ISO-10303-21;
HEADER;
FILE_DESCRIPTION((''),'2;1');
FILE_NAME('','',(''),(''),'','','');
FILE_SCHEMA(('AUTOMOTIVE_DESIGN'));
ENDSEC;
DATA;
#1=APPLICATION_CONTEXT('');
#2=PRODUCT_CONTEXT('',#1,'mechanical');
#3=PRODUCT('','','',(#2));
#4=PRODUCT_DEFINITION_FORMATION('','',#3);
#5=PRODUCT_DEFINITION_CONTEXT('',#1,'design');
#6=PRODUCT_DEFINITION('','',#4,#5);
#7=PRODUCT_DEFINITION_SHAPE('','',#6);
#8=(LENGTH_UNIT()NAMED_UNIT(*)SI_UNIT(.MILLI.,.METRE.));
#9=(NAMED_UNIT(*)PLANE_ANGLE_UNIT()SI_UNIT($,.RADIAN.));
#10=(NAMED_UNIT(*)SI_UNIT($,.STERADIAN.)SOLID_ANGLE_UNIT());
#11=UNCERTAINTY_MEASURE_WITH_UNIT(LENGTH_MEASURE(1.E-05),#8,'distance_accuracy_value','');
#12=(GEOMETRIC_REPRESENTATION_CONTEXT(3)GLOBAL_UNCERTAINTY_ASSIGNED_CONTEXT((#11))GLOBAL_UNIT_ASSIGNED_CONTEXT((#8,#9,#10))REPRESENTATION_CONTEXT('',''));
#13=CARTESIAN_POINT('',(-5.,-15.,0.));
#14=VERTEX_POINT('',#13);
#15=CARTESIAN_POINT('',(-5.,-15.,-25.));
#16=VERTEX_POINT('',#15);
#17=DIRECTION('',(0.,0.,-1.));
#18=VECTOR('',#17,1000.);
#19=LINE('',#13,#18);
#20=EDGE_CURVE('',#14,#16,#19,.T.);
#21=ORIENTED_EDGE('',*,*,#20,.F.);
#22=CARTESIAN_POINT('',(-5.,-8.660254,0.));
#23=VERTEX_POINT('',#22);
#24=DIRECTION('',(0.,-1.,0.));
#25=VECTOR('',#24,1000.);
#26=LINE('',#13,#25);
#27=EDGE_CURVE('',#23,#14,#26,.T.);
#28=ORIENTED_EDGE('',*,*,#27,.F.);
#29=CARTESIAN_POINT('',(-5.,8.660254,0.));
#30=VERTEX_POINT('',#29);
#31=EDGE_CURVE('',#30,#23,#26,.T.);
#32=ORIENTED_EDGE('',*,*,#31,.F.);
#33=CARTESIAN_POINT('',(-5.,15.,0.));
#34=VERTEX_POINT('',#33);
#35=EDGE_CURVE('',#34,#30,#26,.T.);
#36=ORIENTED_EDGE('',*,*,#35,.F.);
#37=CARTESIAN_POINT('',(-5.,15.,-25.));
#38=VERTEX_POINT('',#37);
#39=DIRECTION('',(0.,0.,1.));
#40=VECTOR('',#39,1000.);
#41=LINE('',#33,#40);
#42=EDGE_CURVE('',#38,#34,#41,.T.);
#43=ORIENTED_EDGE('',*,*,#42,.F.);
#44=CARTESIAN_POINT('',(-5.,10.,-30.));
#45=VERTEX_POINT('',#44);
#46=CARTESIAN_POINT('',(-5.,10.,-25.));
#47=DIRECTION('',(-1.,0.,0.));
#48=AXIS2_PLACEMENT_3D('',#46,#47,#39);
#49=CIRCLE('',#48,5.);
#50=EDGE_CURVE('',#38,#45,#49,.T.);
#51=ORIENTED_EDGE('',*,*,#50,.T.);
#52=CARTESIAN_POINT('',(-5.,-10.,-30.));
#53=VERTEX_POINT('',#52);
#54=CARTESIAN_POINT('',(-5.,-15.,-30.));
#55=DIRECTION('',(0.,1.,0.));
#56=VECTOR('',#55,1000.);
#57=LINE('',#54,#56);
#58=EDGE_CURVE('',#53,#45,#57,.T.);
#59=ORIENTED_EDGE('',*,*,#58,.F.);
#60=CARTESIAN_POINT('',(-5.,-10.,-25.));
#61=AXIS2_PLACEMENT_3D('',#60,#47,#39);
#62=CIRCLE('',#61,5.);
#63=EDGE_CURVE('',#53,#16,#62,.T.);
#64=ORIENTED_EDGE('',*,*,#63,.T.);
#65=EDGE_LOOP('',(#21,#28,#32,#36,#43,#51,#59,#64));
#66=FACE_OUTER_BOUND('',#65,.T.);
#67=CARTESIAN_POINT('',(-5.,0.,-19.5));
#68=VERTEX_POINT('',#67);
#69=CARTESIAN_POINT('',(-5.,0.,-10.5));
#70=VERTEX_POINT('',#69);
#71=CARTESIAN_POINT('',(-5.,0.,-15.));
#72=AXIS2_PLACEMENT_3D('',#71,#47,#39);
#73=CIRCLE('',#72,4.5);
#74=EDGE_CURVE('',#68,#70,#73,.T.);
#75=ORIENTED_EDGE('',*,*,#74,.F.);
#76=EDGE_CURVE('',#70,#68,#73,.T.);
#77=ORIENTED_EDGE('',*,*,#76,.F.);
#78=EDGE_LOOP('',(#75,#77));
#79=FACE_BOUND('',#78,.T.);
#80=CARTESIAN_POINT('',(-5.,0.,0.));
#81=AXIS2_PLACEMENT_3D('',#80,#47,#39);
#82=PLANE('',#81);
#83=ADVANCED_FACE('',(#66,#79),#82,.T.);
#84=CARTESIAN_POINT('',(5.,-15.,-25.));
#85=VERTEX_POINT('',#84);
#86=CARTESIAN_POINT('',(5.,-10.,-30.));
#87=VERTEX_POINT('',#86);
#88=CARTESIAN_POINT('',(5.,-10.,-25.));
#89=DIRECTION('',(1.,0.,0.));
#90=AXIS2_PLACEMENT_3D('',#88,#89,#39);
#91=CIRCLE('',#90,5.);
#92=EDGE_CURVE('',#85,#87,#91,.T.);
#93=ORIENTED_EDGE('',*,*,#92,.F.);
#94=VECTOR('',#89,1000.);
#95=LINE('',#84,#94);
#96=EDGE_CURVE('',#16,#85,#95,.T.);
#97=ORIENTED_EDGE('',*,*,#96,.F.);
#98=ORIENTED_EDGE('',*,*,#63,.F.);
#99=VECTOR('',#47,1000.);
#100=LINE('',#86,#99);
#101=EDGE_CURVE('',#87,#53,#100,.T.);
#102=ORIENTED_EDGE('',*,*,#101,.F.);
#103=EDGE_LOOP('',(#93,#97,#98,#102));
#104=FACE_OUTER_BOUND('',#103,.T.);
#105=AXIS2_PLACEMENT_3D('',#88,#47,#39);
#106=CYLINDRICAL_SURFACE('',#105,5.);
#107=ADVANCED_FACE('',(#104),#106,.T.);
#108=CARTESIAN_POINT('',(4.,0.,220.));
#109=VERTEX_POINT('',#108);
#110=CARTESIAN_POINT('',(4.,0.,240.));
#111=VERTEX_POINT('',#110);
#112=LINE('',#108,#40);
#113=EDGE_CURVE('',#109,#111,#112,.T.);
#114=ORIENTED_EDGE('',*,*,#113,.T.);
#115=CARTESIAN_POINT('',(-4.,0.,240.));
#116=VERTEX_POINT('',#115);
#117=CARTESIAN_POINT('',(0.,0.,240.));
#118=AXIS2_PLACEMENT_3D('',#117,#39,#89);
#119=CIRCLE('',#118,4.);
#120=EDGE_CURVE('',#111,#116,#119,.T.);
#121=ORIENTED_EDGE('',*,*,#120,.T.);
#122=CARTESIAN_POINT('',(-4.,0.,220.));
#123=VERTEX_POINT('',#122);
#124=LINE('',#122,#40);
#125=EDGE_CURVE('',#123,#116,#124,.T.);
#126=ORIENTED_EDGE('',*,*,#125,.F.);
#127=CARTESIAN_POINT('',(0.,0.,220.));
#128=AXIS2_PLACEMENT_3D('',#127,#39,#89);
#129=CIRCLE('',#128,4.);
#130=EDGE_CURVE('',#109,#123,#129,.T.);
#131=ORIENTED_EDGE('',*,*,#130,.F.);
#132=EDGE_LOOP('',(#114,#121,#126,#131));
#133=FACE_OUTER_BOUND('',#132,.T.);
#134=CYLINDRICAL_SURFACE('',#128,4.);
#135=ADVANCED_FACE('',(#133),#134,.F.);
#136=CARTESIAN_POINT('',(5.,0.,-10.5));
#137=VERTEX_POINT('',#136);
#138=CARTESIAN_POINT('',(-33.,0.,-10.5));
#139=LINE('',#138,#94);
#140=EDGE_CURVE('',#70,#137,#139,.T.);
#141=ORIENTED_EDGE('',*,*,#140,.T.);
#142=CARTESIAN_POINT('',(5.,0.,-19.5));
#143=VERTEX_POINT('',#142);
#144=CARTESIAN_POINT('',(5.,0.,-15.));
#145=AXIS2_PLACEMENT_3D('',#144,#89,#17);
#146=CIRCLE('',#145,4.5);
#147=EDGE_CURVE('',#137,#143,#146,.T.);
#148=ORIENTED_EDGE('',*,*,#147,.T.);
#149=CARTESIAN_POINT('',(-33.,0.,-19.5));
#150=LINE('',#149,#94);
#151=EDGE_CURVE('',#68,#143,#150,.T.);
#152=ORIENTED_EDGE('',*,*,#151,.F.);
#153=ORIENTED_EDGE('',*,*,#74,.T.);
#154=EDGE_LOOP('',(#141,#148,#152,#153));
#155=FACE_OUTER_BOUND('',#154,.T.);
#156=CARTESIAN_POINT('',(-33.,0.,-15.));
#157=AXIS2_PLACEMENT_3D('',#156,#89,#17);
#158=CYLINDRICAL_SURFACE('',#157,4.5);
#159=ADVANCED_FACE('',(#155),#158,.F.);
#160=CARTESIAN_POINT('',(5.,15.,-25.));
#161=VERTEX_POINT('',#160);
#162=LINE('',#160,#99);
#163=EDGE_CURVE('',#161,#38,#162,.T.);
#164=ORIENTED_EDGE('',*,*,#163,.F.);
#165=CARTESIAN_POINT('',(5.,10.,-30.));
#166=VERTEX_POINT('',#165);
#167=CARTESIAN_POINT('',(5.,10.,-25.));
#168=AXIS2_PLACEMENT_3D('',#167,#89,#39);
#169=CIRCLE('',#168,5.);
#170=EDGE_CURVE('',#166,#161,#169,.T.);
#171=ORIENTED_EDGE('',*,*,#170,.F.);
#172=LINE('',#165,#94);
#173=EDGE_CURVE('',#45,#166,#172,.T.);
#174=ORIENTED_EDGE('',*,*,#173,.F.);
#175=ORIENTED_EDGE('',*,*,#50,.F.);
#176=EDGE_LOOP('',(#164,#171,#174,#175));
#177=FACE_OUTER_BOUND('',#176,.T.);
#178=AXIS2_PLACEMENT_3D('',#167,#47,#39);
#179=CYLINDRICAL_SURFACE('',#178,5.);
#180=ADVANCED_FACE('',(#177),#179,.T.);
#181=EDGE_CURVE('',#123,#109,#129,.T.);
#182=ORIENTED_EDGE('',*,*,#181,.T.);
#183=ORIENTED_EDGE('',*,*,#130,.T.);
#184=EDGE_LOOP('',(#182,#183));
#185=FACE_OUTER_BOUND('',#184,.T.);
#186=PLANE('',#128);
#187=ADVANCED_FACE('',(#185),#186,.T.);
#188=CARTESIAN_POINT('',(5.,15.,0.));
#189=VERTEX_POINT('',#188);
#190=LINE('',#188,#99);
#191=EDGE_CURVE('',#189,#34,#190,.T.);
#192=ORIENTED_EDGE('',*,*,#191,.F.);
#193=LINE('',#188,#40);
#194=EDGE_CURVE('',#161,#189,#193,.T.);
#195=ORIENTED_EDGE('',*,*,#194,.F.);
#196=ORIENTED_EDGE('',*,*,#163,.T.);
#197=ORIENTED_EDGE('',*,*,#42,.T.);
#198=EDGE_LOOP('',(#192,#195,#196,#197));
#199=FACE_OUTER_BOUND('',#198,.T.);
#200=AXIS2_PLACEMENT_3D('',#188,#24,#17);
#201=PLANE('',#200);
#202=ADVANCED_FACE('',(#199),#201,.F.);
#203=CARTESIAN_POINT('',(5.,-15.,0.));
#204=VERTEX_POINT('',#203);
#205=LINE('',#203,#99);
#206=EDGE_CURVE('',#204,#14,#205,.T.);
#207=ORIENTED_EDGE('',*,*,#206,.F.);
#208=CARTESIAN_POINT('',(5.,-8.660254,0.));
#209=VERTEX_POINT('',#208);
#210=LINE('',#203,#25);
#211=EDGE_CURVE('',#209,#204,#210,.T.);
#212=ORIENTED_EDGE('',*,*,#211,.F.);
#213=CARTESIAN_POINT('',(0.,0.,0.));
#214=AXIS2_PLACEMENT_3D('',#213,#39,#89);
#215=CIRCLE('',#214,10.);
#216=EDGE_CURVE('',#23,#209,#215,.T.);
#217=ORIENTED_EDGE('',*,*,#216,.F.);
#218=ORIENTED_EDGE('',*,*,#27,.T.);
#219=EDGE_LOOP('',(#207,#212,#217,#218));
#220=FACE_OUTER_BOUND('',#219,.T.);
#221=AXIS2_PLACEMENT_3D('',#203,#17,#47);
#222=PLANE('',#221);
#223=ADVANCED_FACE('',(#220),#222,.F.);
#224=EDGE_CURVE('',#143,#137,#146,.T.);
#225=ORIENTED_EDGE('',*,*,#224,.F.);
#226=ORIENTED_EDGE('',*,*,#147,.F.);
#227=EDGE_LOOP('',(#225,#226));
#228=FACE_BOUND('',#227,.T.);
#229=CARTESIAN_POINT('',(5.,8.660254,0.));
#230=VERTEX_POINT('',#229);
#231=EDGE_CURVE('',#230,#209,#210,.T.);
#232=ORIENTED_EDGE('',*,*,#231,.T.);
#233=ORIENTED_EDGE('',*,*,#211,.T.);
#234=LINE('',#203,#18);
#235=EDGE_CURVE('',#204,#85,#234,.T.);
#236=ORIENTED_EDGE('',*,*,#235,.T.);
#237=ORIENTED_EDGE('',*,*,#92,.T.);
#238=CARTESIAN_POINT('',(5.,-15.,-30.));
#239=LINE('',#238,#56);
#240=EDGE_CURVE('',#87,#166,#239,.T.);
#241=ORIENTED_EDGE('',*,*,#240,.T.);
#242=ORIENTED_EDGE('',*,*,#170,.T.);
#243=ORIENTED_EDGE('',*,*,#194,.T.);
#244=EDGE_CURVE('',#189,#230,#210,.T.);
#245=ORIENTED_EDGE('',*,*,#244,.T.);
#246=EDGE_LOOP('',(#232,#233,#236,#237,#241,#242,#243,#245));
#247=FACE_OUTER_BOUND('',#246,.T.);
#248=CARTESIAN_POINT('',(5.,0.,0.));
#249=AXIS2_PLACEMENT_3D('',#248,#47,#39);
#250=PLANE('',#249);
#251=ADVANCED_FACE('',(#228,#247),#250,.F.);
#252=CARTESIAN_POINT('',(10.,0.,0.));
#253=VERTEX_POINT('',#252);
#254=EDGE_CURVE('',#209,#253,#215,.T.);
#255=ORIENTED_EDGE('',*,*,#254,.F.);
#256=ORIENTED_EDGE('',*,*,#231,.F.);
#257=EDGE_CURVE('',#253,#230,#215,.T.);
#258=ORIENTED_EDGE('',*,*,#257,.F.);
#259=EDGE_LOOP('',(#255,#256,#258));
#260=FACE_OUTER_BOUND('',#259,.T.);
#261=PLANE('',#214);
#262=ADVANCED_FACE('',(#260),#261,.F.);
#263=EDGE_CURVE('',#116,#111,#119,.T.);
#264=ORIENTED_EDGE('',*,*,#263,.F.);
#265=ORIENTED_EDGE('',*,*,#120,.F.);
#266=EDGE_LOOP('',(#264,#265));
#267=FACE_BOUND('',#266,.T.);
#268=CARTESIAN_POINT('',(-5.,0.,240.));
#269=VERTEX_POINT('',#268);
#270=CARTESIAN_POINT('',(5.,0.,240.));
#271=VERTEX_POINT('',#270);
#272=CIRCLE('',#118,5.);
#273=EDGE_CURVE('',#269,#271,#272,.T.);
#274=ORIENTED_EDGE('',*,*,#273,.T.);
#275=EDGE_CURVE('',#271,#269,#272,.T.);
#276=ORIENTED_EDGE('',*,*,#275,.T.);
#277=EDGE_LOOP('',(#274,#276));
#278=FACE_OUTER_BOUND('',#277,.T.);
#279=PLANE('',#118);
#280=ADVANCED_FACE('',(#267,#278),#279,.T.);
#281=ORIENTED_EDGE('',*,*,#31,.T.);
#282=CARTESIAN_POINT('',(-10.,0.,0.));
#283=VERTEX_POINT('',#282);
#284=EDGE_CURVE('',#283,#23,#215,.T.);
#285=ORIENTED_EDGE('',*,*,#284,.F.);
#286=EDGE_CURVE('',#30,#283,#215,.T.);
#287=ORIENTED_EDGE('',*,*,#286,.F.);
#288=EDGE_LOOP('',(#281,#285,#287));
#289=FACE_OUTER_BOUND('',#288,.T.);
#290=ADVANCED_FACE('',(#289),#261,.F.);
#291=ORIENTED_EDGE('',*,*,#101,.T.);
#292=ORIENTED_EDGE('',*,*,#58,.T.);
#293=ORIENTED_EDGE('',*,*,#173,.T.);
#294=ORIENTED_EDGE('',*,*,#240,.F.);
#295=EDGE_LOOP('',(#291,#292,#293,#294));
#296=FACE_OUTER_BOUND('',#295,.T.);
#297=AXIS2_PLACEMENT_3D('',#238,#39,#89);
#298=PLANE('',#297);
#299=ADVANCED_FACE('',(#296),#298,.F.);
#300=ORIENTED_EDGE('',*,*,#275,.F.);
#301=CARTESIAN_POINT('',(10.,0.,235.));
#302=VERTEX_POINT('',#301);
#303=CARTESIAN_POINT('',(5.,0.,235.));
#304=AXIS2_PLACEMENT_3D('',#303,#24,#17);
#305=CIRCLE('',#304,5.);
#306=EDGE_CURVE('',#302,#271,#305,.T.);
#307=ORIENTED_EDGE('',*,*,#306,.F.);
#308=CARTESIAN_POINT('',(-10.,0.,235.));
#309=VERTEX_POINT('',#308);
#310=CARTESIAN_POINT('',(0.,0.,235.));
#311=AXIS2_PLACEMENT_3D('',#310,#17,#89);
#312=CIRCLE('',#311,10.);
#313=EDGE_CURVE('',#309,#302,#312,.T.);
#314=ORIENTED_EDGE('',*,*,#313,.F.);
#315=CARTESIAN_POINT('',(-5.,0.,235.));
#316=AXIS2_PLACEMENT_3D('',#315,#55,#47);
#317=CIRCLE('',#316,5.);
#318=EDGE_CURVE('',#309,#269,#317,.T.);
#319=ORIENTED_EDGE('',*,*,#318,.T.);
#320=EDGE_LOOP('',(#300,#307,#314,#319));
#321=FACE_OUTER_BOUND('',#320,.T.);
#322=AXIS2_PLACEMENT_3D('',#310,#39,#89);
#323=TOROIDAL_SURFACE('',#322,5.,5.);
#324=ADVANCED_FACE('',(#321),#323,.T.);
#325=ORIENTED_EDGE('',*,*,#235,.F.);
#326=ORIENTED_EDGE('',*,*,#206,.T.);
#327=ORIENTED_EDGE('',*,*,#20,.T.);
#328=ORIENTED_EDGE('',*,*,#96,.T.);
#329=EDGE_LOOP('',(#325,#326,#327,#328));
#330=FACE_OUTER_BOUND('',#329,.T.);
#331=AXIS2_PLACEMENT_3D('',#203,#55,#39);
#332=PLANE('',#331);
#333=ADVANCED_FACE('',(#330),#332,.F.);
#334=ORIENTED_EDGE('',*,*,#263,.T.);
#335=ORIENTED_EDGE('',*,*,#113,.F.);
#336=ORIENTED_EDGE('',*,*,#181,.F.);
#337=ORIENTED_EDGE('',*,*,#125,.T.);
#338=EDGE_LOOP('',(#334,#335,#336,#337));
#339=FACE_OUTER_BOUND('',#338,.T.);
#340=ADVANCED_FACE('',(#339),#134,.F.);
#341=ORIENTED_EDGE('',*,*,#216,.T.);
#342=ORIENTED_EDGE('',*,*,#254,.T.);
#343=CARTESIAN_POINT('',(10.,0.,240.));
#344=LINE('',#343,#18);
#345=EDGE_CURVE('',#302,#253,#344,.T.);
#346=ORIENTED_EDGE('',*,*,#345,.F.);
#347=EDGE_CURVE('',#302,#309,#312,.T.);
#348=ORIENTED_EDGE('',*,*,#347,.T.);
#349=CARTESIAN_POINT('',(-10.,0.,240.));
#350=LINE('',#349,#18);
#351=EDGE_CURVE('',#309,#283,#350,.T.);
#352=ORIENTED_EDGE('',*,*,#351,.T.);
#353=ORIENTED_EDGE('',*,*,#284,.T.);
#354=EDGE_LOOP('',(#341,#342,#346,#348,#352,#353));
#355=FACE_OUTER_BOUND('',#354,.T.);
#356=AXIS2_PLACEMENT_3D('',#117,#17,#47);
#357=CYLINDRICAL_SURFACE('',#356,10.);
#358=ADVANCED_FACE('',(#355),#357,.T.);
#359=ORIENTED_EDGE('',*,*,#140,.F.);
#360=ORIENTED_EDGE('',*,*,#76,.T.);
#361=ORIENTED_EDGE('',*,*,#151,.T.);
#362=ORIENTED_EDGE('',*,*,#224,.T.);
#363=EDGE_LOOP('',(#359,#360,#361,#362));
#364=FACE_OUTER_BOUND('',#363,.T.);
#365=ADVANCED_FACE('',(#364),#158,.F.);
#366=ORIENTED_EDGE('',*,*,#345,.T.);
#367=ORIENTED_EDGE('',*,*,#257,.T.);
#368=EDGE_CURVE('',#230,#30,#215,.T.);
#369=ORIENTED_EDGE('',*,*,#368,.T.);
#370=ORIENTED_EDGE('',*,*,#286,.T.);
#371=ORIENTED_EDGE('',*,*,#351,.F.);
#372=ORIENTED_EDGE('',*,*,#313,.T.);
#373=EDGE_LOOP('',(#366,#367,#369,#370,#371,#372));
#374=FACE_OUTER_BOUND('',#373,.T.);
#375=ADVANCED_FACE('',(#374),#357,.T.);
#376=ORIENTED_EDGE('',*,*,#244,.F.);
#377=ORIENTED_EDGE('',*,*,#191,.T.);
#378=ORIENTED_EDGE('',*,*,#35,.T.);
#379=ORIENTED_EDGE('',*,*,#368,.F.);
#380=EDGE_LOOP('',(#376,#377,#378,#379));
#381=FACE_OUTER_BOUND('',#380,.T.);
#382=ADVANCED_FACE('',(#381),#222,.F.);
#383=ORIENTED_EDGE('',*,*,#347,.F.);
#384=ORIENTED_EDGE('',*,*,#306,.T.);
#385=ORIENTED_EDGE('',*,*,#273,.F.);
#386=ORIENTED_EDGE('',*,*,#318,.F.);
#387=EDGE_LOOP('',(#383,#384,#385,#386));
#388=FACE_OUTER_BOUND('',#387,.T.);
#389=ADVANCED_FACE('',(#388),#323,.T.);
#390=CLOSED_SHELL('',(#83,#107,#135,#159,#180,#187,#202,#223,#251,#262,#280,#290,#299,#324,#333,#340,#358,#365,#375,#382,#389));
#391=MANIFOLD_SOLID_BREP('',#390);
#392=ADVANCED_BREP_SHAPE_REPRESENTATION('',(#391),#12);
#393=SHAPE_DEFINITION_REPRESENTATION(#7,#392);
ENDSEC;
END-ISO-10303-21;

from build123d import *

# Parameters (mm, degrees)
SKETCH1_R           = 10
BOSS_EXTRUDE1_DEPTH = 240
SKETCH2_W           = 30
SKETCH2_H           = 30
BOSS_EXTRUDE2_DEPTH = 5
SKETCH3_R           = 4.5
CUT_EXTRUDE1_DEPTH  = 38
FILLET1_R           = 5
FILLET2_R           = 5
SKETCH4_R           = 4
CUT_EXTRUDE2_DEPTH  = 20


with BuildPart() as part:
    # Sketch1 → Boss-Extrude1 (new body)
    with BuildSketch(Plane.XY):
        Circle(SKETCH1_R)
    extrude(amount=BOSS_EXTRUDE1_DEPTH)

    # Sketch2 → Boss-Extrude2 (add, symmetric)
    with BuildSketch(Plane(origin=(0, 0, 0), x_dir=(0, 0, -1), z_dir=(1, 0, 0))):
        with Locations((15, 0)):
            Rectangle(SKETCH2_W, SKETCH2_H)
    extrude(amount=BOSS_EXTRUDE2_DEPTH, both=True)

    # Sketch3 → Cut-Extrude1 (cut)
    with BuildSketch(Plane(origin=(5, 0, 0), x_dir=(0, 0, -1), z_dir=(1, 0, 0))):
        with Locations((15, 0)):
            Circle(SKETCH3_R)
    extrude(amount=-CUT_EXTRUDE1_DEPTH, mode=Mode.SUBTRACT)

    # Fillet1
    fillet1_edges = [part.edges().sort_by_distance(p)[0] for p in [
        (0, -15, -30),
        (0, 15, -30),
    ]]
    fillet(fillet1_edges, radius=FILLET1_R)

    # Fillet2
    fillet2_edges = [part.edges().sort_by_distance(p)[0] for p in [
        (-10, 0, 240),
    ]]
    fillet(fillet2_edges, radius=FILLET2_R)

    # Sketch4 → Cut-Extrude2 (cut)
    with BuildSketch(Plane.XY.offset(240)):
        Circle(SKETCH4_R)
    extrude(amount=-CUT_EXTRUDE2_DEPTH, mode=Mode.SUBTRACT)


solid = part.part
